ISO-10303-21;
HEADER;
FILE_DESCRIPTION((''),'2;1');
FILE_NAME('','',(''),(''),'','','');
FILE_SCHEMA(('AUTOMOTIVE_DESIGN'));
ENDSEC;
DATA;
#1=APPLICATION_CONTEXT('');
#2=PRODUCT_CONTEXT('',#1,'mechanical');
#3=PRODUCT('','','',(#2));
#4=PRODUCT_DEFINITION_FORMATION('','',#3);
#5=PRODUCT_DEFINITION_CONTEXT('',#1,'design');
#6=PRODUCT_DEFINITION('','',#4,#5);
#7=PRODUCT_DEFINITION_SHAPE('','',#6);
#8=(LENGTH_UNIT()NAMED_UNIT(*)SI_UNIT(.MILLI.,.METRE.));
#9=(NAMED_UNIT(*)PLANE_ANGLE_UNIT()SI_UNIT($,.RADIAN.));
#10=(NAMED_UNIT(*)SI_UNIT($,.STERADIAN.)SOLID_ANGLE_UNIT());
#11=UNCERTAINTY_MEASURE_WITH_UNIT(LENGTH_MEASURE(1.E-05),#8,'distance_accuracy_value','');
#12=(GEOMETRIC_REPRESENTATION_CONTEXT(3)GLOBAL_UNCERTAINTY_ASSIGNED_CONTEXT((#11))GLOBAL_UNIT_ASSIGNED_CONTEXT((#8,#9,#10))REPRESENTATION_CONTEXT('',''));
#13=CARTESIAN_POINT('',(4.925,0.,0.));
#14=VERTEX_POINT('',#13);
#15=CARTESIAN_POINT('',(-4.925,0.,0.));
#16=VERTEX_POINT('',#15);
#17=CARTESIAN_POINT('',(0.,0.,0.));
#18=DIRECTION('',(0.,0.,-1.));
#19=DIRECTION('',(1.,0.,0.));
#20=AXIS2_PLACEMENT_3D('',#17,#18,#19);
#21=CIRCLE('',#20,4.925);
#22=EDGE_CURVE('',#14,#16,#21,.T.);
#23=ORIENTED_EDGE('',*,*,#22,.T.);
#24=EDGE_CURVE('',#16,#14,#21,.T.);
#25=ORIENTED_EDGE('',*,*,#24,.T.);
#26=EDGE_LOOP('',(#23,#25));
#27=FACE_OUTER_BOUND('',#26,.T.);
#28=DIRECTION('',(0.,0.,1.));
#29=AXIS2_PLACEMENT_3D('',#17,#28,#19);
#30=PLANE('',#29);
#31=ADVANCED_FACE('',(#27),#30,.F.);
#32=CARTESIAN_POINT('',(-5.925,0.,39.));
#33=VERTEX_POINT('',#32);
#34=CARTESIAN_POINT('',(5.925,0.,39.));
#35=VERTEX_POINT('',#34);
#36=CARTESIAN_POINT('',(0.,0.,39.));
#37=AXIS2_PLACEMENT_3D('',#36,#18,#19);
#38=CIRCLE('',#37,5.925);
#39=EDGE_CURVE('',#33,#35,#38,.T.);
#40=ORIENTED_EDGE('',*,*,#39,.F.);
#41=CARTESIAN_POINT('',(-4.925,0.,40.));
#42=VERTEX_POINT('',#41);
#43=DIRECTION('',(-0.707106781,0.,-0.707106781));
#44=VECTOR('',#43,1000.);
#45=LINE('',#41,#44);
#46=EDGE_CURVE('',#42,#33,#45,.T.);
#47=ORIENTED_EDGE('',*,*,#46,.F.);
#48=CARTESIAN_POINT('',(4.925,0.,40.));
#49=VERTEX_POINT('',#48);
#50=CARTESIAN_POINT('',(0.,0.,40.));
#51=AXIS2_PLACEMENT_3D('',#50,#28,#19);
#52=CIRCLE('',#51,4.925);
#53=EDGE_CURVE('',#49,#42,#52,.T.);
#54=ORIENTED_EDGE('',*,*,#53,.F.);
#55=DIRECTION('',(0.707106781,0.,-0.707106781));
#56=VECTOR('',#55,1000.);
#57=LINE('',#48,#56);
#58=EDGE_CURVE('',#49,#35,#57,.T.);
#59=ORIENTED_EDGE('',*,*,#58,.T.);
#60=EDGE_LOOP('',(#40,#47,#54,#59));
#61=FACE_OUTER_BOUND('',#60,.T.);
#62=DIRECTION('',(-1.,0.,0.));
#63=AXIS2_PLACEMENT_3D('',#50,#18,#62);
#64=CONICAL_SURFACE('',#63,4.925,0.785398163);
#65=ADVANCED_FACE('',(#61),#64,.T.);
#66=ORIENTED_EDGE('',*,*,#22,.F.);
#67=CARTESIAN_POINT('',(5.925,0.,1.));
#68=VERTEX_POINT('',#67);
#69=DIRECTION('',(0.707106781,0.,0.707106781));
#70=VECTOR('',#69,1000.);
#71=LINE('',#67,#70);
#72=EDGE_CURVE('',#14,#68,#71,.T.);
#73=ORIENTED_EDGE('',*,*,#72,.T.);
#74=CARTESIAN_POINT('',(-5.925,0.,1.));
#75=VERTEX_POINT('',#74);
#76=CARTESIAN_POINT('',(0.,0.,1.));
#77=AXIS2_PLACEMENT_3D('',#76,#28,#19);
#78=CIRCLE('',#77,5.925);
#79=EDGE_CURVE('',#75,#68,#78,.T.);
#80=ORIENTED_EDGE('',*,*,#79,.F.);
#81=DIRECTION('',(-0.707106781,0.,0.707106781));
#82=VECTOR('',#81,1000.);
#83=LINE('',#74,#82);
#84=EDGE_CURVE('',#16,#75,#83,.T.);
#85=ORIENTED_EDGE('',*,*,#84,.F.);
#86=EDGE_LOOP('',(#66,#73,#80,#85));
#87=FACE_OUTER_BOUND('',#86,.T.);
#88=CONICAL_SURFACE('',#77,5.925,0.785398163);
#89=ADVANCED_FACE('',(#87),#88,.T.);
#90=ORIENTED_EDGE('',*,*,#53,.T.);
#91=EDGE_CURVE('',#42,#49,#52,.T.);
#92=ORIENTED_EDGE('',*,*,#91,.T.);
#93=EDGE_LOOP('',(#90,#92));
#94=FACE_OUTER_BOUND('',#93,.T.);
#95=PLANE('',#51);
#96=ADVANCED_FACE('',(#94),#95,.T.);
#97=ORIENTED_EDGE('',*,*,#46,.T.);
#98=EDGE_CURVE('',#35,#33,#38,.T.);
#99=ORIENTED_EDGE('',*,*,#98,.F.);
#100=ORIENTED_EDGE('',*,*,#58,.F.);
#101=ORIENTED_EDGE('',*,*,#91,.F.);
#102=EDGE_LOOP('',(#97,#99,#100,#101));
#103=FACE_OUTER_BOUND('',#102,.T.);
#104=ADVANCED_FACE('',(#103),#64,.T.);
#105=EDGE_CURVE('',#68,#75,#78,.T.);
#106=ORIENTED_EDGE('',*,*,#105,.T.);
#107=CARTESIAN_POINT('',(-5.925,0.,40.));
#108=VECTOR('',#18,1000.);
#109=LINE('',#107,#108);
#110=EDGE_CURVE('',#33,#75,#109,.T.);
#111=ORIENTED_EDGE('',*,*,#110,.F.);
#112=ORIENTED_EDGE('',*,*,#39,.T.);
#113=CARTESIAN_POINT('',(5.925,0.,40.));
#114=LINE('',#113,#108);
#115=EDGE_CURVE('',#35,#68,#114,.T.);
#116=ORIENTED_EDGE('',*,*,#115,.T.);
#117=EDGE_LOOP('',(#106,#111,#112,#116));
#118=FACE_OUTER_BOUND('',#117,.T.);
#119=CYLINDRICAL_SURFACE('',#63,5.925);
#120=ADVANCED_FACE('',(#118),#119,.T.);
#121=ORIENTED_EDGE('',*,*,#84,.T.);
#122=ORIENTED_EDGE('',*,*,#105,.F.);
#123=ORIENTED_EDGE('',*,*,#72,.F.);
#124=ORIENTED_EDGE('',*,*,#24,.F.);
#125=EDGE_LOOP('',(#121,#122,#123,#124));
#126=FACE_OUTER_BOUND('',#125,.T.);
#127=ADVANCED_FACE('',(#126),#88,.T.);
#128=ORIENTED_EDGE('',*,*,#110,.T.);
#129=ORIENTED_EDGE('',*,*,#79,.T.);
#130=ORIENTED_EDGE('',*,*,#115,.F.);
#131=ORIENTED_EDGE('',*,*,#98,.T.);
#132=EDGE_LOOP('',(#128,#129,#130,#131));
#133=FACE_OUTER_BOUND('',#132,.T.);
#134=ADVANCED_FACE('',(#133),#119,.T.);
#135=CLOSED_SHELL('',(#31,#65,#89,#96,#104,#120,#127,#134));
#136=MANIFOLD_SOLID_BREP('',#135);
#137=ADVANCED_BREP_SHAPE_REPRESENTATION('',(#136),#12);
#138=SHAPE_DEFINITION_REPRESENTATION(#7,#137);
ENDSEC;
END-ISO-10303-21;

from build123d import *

# Parameters (mm, degrees)
SKETCH1_R           = 5.925
BOSS_EXTRUDE1_DEPTH = 40
CHAMFER1_SIZE       = 1


with BuildPart() as part:
    # Sketch1 → Boss-Extrude1 (new body)
    with BuildSketch(Plane.XY):
        Circle(SKETCH1_R)
    extrude(amount=BOSS_EXTRUDE1_DEPTH)

    # Chamfer1
    chamfer1_edges = [part.edges().sort_by_distance(p)[0] for p in [
        (-5.925, 0, 0),
        (-5.925, 0, 40),
    ]]
    chamfer(chamfer1_edges, length=CHAMFER1_SIZE)


solid = part.part
